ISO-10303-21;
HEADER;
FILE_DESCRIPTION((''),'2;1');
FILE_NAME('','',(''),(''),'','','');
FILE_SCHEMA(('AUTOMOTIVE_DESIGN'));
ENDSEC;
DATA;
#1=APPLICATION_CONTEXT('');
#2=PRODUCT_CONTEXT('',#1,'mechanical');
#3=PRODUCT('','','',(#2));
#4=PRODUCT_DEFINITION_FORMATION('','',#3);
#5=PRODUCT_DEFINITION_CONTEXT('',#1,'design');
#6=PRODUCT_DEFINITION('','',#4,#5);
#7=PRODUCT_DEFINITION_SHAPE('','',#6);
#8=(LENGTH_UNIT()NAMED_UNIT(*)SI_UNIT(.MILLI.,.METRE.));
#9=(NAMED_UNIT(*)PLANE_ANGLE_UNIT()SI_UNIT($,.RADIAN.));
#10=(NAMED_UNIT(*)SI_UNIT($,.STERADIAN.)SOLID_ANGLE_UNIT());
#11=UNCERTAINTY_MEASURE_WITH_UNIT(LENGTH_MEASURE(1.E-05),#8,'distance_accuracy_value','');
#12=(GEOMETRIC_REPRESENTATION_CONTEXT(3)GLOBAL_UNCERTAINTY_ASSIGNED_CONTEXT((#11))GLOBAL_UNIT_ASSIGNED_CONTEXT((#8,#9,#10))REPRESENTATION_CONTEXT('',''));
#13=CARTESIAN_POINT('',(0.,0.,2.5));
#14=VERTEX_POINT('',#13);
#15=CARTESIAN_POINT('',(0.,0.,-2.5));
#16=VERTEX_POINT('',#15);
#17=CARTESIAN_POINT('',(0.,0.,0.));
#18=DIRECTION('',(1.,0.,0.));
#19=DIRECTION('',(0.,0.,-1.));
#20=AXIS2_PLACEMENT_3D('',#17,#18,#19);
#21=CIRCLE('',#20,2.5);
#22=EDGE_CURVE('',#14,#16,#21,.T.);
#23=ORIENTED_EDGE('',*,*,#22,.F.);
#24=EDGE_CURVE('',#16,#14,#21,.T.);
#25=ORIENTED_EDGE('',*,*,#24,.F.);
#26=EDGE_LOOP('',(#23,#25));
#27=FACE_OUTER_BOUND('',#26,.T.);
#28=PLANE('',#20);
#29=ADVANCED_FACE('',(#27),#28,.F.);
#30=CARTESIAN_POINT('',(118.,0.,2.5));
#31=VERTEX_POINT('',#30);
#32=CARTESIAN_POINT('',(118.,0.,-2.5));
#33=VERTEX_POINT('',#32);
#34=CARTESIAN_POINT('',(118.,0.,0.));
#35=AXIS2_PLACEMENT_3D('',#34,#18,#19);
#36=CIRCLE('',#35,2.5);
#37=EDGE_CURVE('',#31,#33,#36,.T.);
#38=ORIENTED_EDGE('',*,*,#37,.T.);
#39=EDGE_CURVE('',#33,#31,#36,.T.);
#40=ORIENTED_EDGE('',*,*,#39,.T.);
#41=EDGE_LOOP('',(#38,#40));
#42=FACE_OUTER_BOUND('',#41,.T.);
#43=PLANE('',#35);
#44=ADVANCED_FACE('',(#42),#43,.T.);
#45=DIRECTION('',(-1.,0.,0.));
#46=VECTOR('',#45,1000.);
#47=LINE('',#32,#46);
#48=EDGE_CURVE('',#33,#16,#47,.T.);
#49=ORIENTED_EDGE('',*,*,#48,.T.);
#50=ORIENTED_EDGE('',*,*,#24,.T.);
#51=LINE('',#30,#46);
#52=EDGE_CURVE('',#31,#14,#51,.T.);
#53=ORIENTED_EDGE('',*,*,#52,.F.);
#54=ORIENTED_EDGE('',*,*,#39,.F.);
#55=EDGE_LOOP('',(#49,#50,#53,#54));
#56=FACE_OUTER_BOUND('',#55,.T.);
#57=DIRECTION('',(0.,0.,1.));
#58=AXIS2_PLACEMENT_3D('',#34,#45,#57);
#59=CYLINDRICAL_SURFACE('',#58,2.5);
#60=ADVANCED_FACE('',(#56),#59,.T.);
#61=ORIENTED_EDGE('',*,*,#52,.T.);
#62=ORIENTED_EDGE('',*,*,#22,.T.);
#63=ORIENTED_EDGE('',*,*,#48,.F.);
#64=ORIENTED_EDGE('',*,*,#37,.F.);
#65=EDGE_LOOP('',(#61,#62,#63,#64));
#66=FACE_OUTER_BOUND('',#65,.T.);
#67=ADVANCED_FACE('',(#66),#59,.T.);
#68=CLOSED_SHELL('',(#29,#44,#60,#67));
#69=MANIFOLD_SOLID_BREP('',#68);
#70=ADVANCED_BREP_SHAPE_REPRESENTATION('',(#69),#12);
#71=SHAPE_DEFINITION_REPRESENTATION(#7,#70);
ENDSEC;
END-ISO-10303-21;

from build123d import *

# Parameters (mm, degrees)
SKETCH_1_R      = 2.5
EXTRUDE_1_DEPTH = 118


with BuildPart() as part:
    # 草图1 → 凸台-拉伸1 (new body)
    with BuildSketch(Plane(origin=(0, 0, 0), x_dir=(0, 0, -1), z_dir=(1, 0, 0))):
        Circle(SKETCH_1_R)
    extrude(amount=EXTRUDE_1_DEPTH)


solid = part.part
